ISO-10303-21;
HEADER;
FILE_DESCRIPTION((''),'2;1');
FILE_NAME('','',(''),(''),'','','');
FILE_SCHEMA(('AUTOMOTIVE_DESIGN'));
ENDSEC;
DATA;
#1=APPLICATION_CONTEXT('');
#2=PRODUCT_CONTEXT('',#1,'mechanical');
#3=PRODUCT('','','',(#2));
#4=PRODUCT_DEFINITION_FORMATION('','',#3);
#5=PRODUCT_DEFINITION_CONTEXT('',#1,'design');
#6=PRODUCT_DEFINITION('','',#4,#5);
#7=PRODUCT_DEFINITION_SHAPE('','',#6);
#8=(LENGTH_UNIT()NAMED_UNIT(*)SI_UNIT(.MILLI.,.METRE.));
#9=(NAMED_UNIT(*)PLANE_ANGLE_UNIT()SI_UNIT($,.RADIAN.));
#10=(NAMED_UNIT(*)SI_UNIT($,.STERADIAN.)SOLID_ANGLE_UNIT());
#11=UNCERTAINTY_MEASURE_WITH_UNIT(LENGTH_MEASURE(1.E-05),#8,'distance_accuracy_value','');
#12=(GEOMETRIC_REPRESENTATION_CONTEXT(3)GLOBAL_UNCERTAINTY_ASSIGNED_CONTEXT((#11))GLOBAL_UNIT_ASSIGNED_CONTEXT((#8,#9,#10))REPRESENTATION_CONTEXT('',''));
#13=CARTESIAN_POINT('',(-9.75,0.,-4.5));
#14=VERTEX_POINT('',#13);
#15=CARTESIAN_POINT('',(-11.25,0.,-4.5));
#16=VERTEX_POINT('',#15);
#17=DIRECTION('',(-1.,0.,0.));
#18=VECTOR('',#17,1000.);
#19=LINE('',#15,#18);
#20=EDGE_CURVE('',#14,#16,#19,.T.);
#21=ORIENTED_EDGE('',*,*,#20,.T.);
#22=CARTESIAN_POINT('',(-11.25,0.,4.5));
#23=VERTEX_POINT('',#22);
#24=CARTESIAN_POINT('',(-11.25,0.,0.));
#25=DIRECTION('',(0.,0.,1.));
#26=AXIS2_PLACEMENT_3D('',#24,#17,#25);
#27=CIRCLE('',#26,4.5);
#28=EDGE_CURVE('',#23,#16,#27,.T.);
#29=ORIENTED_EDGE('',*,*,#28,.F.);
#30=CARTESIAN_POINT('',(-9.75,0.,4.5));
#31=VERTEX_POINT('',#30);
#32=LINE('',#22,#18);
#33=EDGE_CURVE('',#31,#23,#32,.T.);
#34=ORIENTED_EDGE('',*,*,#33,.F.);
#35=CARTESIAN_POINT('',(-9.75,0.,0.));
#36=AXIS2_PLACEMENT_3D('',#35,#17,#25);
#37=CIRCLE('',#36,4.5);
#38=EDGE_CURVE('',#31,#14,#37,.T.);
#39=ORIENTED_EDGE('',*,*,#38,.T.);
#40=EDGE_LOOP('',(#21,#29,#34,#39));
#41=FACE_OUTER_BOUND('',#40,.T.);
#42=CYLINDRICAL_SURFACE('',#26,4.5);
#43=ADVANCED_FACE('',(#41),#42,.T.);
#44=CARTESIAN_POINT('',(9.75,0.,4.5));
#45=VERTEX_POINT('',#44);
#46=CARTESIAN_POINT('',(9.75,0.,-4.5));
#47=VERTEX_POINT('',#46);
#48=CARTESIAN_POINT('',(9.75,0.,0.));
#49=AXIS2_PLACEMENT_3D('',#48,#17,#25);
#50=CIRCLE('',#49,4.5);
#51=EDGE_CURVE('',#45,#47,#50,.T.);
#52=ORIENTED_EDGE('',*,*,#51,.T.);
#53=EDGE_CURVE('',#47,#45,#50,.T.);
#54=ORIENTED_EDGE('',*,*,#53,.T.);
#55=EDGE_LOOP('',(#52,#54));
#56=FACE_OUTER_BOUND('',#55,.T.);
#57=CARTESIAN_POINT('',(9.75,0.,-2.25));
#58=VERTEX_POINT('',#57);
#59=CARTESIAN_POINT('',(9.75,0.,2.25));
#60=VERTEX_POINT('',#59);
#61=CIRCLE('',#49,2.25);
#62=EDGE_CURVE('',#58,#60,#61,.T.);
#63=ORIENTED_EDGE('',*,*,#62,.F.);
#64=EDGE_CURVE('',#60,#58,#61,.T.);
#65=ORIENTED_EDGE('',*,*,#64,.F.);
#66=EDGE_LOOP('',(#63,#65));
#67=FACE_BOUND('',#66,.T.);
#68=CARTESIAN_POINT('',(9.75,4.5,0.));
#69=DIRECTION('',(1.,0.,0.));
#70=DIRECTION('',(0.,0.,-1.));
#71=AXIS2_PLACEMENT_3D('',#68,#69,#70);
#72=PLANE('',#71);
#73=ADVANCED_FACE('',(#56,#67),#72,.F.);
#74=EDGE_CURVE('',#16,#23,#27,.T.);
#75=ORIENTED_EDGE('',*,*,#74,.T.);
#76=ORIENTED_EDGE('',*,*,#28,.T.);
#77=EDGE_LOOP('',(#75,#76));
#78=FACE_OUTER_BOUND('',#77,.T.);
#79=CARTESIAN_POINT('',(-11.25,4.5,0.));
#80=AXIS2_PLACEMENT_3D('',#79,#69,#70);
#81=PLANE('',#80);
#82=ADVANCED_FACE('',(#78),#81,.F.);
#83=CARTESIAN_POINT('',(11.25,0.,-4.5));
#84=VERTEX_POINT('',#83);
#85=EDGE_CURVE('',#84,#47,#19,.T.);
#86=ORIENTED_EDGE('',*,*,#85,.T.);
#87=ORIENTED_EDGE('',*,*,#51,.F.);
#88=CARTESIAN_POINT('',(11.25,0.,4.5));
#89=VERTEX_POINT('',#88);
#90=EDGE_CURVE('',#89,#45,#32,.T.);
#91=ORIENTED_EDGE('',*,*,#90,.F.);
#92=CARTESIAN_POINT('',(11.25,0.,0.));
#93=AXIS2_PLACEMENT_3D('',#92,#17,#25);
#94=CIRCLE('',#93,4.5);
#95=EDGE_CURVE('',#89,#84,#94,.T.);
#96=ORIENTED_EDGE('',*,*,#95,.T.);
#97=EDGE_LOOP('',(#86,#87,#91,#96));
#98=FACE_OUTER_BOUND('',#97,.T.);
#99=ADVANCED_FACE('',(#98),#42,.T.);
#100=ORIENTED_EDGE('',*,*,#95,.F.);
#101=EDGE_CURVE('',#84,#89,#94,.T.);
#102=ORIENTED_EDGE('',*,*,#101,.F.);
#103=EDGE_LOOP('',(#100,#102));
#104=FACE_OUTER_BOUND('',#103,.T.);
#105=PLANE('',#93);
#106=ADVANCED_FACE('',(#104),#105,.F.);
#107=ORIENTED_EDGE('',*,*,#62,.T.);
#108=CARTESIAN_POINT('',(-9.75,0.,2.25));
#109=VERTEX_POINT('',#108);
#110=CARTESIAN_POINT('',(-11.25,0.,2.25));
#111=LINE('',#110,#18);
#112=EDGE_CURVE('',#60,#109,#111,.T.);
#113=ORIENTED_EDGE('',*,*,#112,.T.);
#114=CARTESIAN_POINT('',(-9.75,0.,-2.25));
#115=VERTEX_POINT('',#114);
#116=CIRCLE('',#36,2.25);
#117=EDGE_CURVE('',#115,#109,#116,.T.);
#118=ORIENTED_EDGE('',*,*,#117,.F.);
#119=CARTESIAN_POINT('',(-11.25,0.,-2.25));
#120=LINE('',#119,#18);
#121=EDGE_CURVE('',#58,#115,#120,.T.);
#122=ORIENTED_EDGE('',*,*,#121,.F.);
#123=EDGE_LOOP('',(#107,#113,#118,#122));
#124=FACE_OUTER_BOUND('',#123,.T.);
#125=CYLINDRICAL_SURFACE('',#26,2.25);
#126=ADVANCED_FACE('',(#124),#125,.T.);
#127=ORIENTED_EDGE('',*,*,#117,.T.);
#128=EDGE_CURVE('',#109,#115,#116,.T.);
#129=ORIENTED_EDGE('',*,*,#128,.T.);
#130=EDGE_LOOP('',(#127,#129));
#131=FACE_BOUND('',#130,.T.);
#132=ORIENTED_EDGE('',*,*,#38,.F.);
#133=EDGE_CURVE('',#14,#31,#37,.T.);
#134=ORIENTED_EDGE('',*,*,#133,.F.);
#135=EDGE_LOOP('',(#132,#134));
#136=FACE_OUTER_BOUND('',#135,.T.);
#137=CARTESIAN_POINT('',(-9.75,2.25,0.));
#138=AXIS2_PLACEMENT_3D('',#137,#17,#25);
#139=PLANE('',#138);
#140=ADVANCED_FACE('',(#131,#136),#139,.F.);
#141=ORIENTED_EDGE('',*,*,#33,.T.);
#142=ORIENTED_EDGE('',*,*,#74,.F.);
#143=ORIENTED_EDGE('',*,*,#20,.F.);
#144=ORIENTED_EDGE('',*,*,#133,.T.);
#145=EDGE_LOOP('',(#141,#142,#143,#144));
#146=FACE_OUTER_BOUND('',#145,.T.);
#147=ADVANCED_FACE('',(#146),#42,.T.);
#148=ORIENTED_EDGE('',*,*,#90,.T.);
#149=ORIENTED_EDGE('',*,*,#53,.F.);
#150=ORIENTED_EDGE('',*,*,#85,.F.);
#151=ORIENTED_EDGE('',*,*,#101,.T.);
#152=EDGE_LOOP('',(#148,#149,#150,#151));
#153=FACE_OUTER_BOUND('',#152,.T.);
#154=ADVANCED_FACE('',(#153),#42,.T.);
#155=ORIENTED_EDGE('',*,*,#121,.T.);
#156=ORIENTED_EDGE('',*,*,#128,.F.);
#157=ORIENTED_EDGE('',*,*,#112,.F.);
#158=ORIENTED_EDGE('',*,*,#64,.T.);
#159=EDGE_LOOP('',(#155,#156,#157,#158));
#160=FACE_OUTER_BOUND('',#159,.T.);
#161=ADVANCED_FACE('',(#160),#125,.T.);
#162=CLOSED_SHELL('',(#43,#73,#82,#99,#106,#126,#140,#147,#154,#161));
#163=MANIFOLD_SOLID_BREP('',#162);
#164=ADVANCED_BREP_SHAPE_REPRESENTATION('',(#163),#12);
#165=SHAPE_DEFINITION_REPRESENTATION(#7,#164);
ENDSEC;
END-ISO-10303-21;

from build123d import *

# Parameters (mm, degrees)
SCALE1_SCALE = 0.3


with BuildPart() as part:
    # Sketch3 → Revolve1 (revolve)
    with BuildSketch(Plane.XY, mode=Mode.PRIVATE) as revolve1_sk:
        Polygon((-37.5, 0), (37.5, 0), (37.5, 15), (32.5, 15), (32.5, 7.5), (-32.5, 7.5), (-32.5, 15), (-37.5, 15), align=None)
    revolve(revolve1_sk.sketch.rotate(Axis((-37.5, 0, 0), (1, 0, 0)), 90), axis=Axis((-37.5, 0, 0), (1, 0, 0)))


with BuildPart() as part_1:
    # Scale1: scaled about (0, 0, 0)
    add(part.part.scale(SCALE1_SCALE))


solid = part_1.part
